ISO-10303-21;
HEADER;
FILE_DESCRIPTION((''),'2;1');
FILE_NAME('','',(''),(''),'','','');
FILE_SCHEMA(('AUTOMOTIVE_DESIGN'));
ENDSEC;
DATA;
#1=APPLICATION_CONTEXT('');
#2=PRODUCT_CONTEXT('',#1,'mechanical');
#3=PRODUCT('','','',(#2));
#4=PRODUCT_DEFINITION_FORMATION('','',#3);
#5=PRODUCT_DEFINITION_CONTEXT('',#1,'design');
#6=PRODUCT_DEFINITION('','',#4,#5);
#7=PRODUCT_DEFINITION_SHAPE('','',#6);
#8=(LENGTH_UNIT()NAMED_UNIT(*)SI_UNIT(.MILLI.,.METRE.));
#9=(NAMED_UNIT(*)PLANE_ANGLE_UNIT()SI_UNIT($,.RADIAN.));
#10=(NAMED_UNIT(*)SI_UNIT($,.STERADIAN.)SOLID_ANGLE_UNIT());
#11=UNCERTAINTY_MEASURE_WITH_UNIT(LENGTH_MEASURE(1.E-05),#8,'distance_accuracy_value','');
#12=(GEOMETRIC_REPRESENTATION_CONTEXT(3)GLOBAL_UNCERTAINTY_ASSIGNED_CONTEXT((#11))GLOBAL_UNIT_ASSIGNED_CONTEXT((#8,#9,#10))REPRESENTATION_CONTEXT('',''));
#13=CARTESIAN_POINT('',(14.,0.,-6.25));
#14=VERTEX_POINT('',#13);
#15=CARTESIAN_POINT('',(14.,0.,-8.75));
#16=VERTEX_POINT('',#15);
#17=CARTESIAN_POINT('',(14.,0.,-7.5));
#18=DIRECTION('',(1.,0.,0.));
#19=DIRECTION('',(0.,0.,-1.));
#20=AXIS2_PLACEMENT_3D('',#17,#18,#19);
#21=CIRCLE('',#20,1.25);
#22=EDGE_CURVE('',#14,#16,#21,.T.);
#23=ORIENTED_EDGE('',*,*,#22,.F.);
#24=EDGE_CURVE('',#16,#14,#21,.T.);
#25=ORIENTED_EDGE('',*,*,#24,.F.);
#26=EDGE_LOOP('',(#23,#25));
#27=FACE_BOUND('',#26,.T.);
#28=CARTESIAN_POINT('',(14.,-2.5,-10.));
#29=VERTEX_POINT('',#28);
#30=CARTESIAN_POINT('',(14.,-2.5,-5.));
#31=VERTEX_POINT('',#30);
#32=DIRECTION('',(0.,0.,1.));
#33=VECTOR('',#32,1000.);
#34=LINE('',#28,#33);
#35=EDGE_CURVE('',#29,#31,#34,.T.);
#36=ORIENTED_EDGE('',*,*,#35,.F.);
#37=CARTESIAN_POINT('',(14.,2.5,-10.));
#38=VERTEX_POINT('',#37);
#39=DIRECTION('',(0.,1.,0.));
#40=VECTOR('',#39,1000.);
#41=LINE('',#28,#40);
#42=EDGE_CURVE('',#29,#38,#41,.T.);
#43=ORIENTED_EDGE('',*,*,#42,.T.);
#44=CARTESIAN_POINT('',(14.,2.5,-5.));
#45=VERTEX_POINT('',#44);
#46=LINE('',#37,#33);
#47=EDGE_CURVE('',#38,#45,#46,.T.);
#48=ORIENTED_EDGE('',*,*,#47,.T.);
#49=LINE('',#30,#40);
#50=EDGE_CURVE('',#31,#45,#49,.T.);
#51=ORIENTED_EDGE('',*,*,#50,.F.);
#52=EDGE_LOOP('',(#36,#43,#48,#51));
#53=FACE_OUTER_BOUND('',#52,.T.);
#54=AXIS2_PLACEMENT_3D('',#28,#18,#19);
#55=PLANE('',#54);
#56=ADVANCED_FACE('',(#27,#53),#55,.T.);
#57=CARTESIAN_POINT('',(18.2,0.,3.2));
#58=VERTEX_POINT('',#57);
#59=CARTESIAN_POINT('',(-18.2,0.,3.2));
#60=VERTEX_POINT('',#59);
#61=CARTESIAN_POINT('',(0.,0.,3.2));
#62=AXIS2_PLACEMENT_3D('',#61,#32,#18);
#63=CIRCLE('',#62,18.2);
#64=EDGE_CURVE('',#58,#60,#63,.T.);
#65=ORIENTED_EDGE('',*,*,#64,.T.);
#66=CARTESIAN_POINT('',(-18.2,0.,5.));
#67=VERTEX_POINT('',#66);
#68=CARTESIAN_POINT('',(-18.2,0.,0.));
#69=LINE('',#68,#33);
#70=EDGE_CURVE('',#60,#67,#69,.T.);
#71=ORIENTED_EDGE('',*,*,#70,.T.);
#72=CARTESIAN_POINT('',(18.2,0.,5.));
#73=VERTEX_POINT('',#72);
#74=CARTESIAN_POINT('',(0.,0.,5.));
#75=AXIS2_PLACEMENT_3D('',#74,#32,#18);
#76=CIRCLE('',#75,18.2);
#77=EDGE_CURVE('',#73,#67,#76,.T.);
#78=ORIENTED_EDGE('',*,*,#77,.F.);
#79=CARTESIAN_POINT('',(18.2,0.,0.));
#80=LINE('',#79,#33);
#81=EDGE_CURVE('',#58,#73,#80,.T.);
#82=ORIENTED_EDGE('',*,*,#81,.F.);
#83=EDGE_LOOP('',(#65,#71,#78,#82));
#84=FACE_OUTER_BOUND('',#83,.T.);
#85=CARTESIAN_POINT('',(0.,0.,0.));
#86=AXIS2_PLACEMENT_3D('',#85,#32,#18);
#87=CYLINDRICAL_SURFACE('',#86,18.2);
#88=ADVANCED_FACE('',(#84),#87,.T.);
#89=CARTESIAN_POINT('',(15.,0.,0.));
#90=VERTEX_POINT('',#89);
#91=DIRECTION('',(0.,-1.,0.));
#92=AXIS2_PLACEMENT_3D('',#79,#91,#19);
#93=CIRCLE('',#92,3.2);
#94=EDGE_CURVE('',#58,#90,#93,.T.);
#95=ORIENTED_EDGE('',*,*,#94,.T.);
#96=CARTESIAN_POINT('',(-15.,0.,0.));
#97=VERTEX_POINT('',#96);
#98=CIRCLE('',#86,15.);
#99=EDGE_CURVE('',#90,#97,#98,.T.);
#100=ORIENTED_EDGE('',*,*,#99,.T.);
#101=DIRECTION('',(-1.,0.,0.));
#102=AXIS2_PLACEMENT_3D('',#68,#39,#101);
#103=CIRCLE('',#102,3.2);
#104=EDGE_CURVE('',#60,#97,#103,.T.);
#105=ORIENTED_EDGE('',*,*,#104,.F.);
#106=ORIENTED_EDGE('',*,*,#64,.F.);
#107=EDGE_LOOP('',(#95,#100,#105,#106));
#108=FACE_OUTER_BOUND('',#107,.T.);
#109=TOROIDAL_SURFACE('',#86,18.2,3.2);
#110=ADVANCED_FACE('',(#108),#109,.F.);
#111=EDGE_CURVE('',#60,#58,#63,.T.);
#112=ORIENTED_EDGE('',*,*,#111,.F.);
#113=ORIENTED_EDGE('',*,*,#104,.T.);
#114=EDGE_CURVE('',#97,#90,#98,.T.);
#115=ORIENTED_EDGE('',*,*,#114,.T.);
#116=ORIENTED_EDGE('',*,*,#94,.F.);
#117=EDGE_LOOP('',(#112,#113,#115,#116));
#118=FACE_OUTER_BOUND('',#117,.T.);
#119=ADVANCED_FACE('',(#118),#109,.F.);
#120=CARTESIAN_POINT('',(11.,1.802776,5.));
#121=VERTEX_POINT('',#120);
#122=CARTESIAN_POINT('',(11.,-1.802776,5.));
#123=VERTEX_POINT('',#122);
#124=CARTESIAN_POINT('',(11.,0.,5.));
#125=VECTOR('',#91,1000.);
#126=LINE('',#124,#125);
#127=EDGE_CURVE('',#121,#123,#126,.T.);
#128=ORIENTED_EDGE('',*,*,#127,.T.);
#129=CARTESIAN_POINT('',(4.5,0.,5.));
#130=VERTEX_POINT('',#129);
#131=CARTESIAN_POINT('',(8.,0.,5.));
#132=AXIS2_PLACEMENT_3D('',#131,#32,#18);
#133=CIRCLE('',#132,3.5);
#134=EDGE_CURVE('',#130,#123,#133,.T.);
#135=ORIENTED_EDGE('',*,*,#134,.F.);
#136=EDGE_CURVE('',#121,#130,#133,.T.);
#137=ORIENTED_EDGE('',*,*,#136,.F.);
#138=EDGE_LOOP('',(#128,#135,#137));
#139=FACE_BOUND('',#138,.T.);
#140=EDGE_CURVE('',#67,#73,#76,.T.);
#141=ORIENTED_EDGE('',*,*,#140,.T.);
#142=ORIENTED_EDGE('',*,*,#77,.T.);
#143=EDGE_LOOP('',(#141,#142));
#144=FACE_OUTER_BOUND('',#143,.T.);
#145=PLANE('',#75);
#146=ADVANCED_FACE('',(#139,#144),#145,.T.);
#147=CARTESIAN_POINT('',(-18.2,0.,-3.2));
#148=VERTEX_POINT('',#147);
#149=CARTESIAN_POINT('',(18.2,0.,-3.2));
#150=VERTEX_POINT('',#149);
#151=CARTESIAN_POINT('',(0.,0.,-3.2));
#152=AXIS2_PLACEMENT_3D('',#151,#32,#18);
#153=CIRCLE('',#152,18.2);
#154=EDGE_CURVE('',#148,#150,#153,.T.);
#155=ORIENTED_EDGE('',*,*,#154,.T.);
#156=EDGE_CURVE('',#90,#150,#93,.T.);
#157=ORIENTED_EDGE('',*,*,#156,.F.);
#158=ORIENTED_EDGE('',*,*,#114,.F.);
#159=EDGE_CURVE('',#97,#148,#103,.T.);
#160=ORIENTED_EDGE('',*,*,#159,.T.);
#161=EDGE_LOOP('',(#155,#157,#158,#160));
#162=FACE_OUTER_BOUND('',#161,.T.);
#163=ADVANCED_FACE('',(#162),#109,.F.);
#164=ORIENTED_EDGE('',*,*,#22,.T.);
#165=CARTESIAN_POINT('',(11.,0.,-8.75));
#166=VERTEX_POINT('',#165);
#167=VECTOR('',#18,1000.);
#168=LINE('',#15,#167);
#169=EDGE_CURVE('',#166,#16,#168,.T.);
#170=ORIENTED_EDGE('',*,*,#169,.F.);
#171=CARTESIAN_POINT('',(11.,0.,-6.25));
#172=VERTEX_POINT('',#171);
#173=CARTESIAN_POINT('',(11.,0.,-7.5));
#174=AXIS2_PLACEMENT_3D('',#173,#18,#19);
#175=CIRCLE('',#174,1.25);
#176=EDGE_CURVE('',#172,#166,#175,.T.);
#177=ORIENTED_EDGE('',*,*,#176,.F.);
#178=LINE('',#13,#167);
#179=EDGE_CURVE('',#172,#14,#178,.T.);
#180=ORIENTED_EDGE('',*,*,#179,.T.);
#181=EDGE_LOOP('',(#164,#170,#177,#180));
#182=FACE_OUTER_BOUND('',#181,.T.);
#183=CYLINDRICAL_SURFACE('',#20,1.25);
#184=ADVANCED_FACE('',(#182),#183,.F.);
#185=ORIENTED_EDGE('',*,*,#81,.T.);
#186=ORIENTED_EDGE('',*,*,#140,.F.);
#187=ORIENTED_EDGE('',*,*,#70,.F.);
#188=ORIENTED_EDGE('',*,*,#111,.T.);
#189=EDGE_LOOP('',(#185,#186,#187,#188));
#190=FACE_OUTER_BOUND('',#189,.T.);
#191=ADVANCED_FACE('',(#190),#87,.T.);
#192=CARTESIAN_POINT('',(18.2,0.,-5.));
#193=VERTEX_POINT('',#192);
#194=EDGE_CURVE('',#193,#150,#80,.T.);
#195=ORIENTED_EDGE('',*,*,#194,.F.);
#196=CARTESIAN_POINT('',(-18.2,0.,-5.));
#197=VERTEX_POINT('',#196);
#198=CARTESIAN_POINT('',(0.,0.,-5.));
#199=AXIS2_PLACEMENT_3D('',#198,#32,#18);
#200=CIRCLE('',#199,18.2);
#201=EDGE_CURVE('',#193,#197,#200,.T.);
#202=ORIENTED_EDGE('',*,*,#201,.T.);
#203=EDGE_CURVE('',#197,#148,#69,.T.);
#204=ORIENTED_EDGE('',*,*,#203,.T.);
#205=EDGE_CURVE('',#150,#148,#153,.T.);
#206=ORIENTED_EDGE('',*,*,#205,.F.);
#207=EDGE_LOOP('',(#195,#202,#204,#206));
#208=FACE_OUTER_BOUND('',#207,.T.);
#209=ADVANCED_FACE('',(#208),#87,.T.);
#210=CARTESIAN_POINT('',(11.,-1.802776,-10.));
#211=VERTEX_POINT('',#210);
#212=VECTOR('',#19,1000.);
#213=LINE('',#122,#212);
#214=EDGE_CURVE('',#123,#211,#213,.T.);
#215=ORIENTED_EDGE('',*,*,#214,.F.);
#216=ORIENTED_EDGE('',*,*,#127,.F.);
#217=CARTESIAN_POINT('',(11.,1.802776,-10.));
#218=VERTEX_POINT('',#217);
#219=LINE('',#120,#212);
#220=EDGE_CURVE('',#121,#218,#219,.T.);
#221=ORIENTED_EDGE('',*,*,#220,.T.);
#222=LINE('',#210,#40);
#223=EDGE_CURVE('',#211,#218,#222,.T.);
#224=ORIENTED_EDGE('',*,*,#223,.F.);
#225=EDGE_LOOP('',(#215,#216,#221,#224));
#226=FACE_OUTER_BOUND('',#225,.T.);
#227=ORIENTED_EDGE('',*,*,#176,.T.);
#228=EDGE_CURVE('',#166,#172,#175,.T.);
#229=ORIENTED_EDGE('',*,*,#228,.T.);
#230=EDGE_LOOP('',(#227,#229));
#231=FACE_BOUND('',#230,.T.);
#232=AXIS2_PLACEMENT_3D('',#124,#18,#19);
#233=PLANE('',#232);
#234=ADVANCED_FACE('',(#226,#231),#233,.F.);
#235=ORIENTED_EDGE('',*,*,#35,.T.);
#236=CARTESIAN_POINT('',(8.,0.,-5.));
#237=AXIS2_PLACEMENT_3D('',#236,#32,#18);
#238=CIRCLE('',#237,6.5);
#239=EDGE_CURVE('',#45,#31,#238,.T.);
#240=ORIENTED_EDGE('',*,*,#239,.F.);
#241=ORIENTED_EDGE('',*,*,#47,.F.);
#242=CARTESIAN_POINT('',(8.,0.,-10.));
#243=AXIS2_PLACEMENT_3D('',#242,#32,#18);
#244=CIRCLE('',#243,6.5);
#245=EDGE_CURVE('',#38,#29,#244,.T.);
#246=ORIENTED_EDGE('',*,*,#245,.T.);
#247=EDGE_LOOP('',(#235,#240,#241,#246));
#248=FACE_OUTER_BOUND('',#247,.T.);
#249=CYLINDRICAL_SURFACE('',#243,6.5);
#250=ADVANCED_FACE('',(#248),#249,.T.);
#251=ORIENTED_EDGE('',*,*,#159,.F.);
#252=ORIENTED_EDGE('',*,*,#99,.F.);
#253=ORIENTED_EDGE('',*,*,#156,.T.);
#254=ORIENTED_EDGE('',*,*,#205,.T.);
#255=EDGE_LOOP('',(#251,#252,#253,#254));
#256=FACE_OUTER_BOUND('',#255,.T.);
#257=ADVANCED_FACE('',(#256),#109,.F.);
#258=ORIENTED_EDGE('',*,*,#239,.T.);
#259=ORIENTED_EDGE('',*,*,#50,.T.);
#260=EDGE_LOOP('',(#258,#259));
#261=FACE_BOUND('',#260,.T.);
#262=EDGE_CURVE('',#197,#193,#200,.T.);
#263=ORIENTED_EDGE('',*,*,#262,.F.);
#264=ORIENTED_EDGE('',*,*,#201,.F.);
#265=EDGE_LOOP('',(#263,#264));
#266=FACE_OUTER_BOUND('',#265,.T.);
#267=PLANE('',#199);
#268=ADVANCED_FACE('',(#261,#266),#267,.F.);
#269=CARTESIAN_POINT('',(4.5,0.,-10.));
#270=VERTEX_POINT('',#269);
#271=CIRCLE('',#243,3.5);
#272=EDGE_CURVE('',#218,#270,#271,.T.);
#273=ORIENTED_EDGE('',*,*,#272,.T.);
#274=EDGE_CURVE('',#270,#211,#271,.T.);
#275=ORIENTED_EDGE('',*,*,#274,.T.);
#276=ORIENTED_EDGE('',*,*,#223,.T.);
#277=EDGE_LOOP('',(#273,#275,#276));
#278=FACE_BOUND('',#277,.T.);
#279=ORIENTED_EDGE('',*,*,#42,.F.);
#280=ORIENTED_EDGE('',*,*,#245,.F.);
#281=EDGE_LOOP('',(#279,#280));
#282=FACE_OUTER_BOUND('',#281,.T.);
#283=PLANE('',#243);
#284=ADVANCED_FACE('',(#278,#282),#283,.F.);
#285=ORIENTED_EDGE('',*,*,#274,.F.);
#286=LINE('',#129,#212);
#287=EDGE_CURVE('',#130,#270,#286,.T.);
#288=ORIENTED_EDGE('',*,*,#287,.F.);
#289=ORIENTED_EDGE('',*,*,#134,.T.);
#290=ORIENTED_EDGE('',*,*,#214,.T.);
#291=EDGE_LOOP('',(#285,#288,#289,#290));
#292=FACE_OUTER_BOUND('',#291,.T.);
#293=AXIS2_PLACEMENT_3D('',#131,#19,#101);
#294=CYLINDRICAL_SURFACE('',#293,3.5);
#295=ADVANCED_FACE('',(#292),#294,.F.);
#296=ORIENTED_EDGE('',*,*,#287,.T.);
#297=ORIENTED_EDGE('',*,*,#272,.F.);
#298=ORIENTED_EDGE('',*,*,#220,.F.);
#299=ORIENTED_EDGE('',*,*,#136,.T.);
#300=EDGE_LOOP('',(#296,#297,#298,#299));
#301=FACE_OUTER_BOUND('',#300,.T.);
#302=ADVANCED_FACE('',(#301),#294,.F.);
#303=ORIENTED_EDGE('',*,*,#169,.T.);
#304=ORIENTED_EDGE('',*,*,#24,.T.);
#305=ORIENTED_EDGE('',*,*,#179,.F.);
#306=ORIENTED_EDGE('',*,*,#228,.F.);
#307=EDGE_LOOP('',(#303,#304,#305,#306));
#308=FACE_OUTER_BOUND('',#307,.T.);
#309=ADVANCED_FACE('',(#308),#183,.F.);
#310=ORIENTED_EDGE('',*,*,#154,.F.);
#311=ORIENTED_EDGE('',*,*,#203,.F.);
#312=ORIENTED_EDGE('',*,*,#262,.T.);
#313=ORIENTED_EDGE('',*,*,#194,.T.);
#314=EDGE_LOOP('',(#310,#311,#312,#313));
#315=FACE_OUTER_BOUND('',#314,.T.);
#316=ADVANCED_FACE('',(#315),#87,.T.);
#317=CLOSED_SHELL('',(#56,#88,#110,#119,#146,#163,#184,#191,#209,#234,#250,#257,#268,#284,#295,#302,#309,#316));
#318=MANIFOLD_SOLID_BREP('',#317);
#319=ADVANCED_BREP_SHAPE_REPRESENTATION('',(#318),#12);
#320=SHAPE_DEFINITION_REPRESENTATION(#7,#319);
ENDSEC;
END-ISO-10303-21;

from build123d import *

# Parameters (mm, degrees)
SKETCH_1_R      = 15
EXTRUDE_1_DEPTH = 5
EXTRUDE_2_DEPTH = 5
M3X0_5_1_D      = 2.5
M3X0_5_1_DEPTH  = 7.5
M3X0_5_1_TIP    = 0.751075774


with BuildPart() as part:
    # 草图1 → 凸台-拉伸1 (new, symmetric)
    with BuildSketch(Plane.XY):
        Circle(SKETCH_1_R)
        with BuildLine():
            Line((11, 1.802775638), (11, -1.802775638))
            ThreePointArc((11, -1.802775638), (4.5, 0), (11, 1.802775638))
        make_face(mode=Mode.SUBTRACT)
    extrude(amount=EXTRUDE_1_DEPTH, both=True)

    # 草图4 → 旋转1 (revolve)
    with BuildSketch(Plane(origin=(0, 0, 0), x_dir=(1, 0, 0), z_dir=(0, 1, 0))):
        with BuildLine():
            Line((18.2, 5), (15, 5))
            Line((15, 5), (15, 0))
            ThreePointArc((15, 0), (15.9372583, 2.2627417), (18.2, 3.2))
            Line((18.2, 3.2), (18.2, 5))
        make_face()
        with BuildLine():
            ThreePointArc((18.2, -3.2), (15.9372583, -2.2627417), (15, 0))
            Line((15, 0), (15, -5))
            Line((15, -5), (18.2, -5))
            Line((18.2, -5), (18.2, -3.2))
        make_face()
    revolve(axis=Axis((0, 0, 0), (0, 0, -1)))

    # 草图5 → 凸台-拉伸2 (add)
    with BuildSketch(Plane.XY.offset(-5)):
        with BuildLine():
            Line((14, -2.5), (14, 2.5))
            ThreePointArc((14, 2.5), (1.5, 0), (14, -2.5))
        make_face()
        with BuildLine():
            Line((11, -1.802775638), (11, 1.802775638))
            ThreePointArc((11, 1.802775638), (4.5, 0), (11, -1.802775638))
        make_face(mode=Mode.SUBTRACT)
    extrude(amount=-EXTRUDE_2_DEPTH)

    # M3x0.5 螺纹孔1
    with Locations(Plane(origin=(14, 0, -7.5), x_dir=(0, 0, 1), z_dir=(1, 0, 0))):
        with Locations((0, 0)):
            Hole(M3X0_5_1_D / 2, depth=M3X0_5_1_DEPTH)
            with Locations((0, 0, -(M3X0_5_1_DEPTH + M3X0_5_1_TIP / 2))):  # 118° drill point
                Cone(0, M3X0_5_1_D / 2, M3X0_5_1_TIP, mode=Mode.SUBTRACT)


solid = part.part
